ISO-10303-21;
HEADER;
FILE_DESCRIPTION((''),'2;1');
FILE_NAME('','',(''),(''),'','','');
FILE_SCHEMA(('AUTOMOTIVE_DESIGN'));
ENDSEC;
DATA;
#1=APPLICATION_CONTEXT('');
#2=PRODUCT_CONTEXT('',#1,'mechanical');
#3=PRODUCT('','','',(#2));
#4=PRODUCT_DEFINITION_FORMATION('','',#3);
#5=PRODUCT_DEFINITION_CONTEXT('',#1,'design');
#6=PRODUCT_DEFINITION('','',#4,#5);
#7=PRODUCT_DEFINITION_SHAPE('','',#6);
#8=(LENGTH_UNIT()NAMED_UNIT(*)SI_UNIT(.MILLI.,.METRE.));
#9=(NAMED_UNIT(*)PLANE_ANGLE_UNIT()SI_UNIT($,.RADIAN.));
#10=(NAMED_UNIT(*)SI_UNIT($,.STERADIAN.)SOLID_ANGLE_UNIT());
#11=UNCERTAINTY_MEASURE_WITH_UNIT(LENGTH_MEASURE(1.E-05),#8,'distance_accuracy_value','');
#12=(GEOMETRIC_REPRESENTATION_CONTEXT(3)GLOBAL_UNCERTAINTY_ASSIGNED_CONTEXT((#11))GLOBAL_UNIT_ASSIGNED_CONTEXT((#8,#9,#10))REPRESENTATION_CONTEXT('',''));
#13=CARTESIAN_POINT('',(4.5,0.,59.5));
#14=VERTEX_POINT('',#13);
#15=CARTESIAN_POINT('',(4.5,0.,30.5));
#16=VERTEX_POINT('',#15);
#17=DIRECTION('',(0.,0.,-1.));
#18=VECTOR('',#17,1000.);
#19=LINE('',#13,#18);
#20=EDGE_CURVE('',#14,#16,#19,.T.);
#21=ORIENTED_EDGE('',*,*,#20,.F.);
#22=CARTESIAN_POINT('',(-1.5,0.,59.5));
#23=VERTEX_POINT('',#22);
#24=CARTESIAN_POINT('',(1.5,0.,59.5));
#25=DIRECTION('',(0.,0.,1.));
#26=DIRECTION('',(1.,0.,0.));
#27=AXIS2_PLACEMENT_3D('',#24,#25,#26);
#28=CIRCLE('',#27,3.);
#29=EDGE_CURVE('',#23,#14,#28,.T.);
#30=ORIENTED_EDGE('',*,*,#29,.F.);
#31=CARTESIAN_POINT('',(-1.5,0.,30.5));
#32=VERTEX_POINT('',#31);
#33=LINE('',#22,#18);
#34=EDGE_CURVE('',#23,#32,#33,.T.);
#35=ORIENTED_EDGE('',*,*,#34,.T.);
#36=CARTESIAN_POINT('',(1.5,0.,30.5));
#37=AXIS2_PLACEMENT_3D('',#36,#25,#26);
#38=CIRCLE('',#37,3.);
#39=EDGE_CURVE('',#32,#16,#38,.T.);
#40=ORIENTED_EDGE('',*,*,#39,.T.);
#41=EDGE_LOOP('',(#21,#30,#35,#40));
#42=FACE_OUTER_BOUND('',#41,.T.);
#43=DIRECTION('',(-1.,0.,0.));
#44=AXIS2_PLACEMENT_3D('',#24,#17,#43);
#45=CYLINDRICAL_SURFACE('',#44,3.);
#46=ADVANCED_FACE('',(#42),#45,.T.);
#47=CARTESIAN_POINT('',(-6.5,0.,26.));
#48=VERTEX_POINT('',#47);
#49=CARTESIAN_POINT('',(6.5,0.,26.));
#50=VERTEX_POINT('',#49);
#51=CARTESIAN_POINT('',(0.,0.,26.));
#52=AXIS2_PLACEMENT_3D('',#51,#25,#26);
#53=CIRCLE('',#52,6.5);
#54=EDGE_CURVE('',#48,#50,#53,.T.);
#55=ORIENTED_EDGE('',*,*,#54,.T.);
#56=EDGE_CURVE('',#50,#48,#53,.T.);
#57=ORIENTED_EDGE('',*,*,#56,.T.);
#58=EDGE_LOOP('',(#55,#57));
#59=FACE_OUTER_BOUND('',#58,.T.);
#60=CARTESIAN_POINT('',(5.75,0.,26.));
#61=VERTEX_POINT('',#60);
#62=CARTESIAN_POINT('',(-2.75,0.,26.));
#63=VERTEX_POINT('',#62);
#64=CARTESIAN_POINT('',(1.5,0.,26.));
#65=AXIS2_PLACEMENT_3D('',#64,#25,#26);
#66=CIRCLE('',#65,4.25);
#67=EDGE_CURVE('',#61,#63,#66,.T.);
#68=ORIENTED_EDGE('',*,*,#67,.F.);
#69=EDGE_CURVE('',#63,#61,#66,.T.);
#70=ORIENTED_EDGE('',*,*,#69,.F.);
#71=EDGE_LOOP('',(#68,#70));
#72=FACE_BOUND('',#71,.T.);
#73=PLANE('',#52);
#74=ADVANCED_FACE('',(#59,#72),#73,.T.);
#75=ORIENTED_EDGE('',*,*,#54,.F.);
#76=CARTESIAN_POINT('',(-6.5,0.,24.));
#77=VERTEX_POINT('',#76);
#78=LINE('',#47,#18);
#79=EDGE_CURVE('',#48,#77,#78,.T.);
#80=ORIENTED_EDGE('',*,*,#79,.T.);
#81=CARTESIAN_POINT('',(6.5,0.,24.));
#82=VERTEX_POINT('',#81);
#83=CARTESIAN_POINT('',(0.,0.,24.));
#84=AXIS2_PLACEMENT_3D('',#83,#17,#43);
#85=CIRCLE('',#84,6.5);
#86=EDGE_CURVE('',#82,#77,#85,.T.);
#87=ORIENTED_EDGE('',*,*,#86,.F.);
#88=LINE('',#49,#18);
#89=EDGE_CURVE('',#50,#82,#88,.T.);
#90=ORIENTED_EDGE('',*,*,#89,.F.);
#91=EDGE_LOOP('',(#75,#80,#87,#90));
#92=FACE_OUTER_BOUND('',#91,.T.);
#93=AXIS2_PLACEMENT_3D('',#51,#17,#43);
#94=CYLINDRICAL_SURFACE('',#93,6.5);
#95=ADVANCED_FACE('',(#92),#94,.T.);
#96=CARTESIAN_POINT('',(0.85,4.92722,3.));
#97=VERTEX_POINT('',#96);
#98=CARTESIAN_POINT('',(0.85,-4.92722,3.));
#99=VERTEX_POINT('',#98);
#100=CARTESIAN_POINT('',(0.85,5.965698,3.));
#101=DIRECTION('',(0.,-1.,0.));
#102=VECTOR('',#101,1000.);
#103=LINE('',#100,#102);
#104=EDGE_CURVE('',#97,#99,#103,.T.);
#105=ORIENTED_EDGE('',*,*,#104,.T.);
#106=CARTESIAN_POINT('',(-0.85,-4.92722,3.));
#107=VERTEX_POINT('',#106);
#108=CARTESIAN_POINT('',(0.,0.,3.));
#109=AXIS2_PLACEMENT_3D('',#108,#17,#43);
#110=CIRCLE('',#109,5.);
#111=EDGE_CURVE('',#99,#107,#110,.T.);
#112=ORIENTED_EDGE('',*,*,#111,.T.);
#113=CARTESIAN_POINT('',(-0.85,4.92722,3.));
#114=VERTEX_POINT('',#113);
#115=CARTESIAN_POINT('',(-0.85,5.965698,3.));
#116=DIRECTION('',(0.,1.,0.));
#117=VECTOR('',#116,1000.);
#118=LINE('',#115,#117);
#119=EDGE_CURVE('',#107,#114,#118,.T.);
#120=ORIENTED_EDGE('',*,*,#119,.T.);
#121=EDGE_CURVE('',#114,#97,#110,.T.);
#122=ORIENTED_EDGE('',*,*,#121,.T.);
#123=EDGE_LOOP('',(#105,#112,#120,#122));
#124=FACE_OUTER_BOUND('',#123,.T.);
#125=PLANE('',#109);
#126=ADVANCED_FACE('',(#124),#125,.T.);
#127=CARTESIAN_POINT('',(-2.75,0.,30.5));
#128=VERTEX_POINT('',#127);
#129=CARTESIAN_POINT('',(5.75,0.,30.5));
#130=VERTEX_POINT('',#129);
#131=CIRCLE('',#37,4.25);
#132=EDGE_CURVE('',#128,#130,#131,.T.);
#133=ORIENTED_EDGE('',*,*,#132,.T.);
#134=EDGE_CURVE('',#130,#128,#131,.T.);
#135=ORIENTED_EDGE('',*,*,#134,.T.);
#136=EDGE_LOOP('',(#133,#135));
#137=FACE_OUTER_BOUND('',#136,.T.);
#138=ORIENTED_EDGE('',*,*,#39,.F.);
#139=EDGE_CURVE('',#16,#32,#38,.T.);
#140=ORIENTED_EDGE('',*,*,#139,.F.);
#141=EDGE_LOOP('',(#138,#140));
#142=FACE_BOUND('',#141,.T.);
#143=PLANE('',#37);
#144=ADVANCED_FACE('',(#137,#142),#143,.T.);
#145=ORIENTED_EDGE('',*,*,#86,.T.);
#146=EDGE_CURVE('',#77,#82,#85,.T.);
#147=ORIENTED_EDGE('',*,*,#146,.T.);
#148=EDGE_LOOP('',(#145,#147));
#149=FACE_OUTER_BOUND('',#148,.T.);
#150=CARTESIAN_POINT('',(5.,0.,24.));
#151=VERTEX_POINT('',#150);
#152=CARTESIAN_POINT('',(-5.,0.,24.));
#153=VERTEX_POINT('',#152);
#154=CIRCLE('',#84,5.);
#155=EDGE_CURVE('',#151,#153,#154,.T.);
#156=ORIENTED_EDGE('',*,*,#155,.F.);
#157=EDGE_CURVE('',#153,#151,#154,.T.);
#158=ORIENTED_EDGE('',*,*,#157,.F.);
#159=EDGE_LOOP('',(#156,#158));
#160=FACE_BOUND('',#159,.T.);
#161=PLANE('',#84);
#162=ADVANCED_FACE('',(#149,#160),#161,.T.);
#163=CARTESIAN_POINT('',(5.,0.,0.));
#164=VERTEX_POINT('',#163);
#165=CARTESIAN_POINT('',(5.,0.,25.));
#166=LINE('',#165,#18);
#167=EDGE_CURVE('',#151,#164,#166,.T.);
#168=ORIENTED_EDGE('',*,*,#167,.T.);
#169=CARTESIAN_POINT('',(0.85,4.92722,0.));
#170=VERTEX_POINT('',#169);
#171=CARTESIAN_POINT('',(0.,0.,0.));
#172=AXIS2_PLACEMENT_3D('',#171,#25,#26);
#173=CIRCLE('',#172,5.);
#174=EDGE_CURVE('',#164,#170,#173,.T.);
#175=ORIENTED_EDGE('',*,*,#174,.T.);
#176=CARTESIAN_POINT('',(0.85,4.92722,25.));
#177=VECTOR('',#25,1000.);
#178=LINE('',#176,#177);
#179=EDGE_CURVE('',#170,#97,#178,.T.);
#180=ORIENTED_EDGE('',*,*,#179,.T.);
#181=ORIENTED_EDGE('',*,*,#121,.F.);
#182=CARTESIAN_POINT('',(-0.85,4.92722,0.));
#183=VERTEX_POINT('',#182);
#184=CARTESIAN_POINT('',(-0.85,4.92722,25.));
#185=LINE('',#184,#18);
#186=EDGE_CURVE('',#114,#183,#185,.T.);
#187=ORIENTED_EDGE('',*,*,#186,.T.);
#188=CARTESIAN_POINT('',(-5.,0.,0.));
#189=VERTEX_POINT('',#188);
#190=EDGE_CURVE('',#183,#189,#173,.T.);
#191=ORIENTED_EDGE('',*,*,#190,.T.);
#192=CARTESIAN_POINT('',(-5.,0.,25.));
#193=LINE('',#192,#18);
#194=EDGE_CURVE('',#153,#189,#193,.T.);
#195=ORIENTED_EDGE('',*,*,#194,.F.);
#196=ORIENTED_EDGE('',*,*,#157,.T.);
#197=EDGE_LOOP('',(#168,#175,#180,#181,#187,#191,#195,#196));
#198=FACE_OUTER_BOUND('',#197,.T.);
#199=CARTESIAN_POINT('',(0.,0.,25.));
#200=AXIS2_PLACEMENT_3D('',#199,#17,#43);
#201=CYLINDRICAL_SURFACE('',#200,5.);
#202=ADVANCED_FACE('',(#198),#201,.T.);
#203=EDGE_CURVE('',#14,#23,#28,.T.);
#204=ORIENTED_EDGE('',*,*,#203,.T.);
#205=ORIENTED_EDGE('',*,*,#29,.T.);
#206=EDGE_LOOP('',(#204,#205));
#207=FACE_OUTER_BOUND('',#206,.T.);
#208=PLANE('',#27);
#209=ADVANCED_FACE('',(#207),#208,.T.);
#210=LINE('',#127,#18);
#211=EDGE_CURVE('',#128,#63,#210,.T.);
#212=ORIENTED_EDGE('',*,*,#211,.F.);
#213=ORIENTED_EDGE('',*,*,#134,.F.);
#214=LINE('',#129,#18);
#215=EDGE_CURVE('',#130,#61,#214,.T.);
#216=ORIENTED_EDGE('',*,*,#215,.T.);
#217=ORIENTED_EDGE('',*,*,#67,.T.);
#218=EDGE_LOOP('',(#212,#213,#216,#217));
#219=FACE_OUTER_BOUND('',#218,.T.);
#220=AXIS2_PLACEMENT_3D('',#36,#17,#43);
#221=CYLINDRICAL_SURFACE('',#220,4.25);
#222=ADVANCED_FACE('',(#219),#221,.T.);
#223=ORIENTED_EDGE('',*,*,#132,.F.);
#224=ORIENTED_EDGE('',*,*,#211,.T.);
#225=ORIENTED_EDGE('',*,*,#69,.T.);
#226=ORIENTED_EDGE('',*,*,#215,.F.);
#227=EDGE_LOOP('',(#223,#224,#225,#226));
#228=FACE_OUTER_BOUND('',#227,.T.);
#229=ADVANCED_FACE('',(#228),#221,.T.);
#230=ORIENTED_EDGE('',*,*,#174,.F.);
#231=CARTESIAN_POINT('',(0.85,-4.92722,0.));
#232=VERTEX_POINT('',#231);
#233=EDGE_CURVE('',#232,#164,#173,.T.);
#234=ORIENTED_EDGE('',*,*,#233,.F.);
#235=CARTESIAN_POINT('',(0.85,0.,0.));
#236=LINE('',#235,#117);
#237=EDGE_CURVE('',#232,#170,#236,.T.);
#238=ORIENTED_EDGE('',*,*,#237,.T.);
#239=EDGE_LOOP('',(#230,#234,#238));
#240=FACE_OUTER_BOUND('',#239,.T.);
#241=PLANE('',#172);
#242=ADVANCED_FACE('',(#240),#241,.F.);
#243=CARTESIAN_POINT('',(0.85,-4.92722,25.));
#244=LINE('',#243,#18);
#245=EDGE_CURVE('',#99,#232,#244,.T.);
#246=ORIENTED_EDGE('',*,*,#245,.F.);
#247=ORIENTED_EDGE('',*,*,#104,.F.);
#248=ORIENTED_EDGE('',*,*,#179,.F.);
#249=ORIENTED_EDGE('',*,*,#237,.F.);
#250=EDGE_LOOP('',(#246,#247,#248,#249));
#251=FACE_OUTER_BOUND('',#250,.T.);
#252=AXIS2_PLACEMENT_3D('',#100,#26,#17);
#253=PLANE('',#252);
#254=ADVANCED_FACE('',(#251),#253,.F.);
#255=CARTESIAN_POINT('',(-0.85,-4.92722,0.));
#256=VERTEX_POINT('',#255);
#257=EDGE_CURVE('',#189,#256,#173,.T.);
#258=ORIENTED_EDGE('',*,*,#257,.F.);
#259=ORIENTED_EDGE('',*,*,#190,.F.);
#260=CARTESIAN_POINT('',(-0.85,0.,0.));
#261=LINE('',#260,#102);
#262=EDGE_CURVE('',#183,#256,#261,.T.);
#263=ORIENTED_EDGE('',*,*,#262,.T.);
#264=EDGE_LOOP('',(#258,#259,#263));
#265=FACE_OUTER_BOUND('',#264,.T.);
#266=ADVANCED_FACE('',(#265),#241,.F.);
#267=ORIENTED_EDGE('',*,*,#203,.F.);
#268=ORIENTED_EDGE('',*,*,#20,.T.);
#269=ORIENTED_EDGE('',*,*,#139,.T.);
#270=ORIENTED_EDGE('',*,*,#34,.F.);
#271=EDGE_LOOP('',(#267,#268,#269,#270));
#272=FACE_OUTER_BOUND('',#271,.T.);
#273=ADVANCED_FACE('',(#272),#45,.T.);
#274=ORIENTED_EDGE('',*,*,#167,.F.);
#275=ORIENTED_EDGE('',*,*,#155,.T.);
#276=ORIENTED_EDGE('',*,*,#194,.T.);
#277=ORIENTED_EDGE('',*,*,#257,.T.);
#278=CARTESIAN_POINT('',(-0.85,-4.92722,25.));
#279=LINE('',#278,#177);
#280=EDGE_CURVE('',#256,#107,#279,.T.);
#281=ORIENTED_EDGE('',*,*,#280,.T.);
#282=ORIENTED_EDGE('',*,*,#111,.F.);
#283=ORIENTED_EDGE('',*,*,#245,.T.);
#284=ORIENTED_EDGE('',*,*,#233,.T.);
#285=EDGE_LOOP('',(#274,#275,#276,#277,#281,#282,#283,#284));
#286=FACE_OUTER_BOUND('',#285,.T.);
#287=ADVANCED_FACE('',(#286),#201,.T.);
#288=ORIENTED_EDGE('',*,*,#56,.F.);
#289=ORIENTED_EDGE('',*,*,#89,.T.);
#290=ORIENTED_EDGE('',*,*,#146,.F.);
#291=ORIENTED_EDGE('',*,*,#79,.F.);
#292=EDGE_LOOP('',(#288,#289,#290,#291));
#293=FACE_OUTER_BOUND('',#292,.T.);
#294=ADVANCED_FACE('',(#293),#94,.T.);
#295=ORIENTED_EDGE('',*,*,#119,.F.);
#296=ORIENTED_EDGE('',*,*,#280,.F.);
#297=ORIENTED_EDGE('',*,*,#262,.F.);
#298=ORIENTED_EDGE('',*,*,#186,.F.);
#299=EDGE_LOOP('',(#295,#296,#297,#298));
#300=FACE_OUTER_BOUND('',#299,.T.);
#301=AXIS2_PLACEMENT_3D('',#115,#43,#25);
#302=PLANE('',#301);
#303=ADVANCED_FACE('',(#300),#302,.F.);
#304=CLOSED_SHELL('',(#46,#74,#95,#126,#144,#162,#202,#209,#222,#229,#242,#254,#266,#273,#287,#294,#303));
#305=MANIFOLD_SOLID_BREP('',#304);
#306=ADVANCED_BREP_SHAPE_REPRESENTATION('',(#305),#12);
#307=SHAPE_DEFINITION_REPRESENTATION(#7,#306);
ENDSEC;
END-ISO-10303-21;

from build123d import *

# Parameters (mm, degrees)
SKETCH1_R           = 5
BOSS_EXTRUDE1_DEPTH = 25
SKETCH2_R           = 6.5
BOSS_EXTRUDE2_DEPTH = 1
SKETCH3_R           = 4.25
BOSS_EXTRUDE3_DEPTH = 4.5
SKETCH4_R           = 3
BOSS_EXTRUDE4_DEPTH = 29
SKETCH6_W           = 1.7
SKETCH6_H           = 11.931395552
CUT_EXTRUDE1_DEPTH  = 3
BOSS_EXTRUDE5_START = 1
SKETCH7_R           = 6.5
BOSS_EXTRUDE5_DEPTH = 1


with BuildPart() as part:
    # Sketch1 → Boss-Extrude1 (new body)
    with BuildSketch(Plane.XY):
        Circle(SKETCH1_R)
    extrude(amount=BOSS_EXTRUDE1_DEPTH)

    # Sketch2 → Boss-Extrude2 (add)
    with BuildSketch(Plane.XY.offset(25)):
        Circle(SKETCH2_R)
    extrude(amount=BOSS_EXTRUDE2_DEPTH)

    # Sketch3 → Boss-Extrude3 (add)
    with BuildSketch(Plane.XY.offset(26)):
        with Locations((1.5, 0)):
            Circle(SKETCH3_R)
    extrude(amount=BOSS_EXTRUDE3_DEPTH)

    # Sketch4 → Boss-Extrude4 (add)
    with BuildSketch(Plane.XY.offset(30.5)):
        with Locations(Location((1.5, 0, 0), (0, 0, 180))):
            Circle(SKETCH4_R)
    extrude(amount=BOSS_EXTRUDE4_DEPTH)

    # Sketch6 → Cut-Extrude1 (cut)
    with BuildSketch(Plane(origin=(0, 0, 0), x_dir=(-1, 0, 0), z_dir=(0, 0, -1))):
        Rectangle(SKETCH6_W, SKETCH6_H)
    extrude(amount=-CUT_EXTRUDE1_DEPTH, mode=Mode.SUBTRACT)

    # Sketch7 → Boss-Extrude5 (add)
    with BuildSketch(Plane(origin=(0, 0, 25), x_dir=(-1, 0, 0), z_dir=(0, 0, -1)).offset(BOSS_EXTRUDE5_START)):
        Circle(SKETCH7_R)
    extrude(amount=-BOSS_EXTRUDE5_DEPTH)


solid = part.part
